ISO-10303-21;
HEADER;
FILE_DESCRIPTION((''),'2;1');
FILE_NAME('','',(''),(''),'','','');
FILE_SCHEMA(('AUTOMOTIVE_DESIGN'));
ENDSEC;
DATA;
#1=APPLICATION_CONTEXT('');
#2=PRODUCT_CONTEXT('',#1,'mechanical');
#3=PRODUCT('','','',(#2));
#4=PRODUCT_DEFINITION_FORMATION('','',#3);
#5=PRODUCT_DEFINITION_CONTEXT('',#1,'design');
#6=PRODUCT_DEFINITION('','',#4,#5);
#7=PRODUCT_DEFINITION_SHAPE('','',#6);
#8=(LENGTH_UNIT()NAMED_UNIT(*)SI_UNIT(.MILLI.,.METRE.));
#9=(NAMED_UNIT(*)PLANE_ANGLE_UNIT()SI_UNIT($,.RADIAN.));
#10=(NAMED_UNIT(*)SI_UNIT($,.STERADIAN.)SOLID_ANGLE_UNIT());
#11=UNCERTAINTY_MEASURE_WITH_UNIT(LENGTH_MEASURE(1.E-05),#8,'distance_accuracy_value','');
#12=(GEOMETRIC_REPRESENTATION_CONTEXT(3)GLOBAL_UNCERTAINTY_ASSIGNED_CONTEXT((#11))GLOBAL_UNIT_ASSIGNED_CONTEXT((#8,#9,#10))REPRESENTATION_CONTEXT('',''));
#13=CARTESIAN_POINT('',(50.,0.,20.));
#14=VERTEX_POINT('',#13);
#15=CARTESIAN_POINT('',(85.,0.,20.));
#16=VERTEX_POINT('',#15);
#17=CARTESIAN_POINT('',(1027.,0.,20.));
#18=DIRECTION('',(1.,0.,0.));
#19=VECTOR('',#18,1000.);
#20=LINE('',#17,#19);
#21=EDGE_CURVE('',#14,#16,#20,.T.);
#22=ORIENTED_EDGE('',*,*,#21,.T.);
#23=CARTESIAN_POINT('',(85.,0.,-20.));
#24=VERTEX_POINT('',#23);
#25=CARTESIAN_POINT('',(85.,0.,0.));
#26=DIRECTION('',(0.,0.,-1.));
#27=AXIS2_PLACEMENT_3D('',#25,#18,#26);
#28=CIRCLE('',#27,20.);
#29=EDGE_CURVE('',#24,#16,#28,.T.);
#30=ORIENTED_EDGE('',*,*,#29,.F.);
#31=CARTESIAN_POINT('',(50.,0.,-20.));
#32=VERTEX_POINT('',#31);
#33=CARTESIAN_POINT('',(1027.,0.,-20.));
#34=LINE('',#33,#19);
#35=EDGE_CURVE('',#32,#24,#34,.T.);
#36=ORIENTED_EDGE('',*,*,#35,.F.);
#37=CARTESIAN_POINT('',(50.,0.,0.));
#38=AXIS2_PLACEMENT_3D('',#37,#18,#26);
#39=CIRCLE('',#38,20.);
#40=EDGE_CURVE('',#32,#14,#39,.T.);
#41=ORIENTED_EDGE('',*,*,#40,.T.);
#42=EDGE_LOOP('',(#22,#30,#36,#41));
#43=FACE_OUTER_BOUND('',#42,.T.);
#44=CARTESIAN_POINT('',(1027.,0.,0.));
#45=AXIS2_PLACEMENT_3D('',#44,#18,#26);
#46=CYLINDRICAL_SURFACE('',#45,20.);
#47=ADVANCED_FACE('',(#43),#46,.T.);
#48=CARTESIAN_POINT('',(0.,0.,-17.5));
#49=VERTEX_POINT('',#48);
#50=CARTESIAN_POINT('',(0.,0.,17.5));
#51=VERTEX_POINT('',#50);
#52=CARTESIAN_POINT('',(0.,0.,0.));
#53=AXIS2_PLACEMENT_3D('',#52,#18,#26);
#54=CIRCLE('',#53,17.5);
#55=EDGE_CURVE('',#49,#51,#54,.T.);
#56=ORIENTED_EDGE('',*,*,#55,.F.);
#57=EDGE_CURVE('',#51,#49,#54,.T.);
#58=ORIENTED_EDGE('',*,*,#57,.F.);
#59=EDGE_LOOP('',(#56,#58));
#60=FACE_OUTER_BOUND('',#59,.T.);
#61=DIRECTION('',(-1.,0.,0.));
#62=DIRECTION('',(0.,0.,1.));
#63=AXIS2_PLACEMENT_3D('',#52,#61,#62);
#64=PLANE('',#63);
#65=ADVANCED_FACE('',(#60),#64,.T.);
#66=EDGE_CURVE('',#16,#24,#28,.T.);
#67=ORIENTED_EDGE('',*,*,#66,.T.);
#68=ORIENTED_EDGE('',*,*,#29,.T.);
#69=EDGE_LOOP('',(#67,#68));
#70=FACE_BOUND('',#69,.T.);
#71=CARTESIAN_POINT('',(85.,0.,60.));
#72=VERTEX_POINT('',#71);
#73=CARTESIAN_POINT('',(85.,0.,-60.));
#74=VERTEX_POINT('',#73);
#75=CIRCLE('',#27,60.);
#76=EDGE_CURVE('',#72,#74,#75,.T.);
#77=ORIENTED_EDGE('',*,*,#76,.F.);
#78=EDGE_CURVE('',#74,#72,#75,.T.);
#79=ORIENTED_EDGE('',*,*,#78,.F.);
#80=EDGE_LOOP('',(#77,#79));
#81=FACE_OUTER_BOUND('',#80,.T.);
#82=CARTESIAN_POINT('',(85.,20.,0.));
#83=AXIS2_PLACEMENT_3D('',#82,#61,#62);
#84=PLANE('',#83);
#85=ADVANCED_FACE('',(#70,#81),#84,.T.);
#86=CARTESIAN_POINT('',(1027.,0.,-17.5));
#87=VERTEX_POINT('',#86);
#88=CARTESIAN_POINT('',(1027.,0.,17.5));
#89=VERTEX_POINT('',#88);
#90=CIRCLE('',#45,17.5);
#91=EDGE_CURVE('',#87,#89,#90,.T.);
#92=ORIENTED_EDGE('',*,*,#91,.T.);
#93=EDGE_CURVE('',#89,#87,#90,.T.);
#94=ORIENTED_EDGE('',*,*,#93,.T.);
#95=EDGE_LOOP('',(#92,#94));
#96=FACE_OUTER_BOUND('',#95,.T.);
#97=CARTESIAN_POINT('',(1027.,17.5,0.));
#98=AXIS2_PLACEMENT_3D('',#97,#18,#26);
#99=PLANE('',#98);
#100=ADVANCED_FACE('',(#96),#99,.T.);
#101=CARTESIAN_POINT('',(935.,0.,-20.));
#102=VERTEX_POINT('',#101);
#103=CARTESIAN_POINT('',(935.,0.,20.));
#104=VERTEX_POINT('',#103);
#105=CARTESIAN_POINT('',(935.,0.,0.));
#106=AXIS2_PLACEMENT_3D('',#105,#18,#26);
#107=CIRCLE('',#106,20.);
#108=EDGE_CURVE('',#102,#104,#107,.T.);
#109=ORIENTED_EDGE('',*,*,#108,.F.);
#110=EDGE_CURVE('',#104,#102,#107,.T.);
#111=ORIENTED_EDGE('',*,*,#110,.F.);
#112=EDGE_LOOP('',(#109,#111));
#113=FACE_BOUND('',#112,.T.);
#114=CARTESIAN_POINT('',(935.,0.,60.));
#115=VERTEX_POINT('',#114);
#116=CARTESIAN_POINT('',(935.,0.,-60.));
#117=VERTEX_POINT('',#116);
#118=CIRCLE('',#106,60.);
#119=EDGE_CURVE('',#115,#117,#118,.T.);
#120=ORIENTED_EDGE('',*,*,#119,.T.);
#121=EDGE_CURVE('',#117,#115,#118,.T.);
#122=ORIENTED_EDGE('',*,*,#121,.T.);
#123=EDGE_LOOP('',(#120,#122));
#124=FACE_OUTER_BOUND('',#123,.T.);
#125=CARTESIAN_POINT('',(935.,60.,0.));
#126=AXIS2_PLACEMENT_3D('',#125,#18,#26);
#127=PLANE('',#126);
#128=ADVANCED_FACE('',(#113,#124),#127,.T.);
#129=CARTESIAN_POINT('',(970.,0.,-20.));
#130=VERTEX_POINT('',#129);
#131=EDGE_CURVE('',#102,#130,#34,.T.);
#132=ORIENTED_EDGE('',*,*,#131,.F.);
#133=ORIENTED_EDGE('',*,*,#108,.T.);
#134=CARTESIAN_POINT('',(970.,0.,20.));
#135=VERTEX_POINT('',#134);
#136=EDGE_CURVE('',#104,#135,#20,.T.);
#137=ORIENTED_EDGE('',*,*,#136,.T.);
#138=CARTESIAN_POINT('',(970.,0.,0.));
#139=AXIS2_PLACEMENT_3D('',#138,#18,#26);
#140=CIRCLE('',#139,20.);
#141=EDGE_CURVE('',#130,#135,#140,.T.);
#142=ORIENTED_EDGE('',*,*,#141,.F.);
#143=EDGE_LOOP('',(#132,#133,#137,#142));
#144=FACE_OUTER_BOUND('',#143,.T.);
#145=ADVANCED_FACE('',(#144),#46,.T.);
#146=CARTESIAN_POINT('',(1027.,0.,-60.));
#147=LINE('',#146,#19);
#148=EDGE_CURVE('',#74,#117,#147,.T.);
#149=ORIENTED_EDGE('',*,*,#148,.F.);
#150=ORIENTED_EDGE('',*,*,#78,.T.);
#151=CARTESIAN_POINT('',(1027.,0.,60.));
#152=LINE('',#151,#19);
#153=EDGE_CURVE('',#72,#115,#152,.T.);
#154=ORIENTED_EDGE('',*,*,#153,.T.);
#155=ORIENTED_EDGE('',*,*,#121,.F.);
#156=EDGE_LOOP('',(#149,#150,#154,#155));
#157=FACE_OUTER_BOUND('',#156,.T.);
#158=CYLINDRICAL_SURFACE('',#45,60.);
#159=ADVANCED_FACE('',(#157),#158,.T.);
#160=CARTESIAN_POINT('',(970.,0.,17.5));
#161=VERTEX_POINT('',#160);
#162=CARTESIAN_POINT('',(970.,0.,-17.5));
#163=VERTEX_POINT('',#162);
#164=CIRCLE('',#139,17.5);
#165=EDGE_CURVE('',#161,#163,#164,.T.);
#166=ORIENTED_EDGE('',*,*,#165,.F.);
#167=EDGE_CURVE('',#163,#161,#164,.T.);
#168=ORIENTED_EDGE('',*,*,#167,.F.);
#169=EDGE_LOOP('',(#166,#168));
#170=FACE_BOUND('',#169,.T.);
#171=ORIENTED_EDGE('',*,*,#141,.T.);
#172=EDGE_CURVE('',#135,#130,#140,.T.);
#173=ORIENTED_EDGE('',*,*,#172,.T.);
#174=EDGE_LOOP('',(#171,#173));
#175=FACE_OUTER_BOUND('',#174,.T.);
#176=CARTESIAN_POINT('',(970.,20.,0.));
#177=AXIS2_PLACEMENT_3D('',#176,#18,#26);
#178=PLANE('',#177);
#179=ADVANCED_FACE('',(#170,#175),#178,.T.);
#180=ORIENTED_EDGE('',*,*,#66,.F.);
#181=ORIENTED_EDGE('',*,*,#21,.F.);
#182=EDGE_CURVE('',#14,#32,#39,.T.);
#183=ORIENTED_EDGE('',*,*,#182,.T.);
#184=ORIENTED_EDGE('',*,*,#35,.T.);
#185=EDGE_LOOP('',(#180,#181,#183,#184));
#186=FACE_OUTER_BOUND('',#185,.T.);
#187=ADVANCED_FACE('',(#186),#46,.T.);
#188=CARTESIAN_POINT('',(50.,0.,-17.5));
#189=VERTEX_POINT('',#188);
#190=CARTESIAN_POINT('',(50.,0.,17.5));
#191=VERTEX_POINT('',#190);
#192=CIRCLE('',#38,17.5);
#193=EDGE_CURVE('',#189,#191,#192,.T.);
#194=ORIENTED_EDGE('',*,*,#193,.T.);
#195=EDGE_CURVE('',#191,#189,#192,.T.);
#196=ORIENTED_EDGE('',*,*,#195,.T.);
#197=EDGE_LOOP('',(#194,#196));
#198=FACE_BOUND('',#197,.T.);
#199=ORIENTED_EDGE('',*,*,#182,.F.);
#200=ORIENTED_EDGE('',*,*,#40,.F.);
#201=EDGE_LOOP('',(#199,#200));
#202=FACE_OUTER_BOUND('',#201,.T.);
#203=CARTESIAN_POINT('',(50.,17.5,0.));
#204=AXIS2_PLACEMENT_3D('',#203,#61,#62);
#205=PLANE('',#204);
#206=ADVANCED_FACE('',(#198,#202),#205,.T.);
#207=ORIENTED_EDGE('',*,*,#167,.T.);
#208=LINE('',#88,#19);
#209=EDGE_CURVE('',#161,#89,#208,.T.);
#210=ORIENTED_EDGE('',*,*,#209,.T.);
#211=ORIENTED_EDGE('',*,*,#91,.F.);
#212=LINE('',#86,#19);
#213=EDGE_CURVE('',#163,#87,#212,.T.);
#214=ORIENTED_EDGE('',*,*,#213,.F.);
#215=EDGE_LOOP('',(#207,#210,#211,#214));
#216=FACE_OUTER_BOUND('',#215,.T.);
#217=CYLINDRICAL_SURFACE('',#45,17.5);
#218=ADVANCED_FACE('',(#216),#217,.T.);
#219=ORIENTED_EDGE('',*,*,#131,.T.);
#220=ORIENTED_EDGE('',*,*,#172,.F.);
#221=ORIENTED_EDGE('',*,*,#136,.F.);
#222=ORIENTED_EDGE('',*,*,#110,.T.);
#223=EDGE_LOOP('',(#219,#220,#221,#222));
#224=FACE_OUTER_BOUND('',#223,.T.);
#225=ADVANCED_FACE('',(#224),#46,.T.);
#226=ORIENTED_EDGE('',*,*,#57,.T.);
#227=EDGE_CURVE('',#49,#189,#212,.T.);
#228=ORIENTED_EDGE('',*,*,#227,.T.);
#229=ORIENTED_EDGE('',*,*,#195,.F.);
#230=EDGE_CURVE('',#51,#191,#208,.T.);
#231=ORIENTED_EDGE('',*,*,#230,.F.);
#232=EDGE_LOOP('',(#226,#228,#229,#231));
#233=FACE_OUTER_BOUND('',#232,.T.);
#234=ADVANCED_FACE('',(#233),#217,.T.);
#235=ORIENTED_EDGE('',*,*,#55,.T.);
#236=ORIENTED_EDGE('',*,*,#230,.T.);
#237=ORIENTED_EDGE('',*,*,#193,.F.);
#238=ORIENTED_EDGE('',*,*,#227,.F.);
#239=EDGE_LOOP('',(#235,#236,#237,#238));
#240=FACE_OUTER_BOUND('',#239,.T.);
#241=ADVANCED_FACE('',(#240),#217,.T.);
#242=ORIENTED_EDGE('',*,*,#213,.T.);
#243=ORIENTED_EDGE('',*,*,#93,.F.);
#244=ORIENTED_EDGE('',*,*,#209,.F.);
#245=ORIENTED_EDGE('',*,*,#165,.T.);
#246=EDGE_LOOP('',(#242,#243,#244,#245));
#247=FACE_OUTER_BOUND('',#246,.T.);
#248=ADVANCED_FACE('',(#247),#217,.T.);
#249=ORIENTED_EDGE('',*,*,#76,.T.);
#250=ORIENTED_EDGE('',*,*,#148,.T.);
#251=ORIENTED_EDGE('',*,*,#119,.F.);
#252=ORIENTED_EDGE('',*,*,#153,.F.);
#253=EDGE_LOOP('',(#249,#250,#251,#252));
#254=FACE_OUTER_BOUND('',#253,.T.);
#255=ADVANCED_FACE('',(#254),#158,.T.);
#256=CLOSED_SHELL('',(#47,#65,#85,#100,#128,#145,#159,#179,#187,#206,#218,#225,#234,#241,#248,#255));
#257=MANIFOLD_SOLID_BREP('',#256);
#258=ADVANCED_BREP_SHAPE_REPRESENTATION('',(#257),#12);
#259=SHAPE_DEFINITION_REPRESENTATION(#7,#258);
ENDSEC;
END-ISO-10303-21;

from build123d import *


with BuildPart() as part:
    # 草图1 → 旋转1 (revolve)
    with BuildSketch(Plane.XY, mode=Mode.PRIVATE) as revolve_1_sk:
        Polygon((0, 0), (0, 17.5), (50, 17.5), (50, 20), (85, 20), (85, 60), (935, 60), (935, 20), (970, 20), (970, 17.5), (1027, 17.5), (1027, 0), align=None)
    revolve(revolve_1_sk.sketch.rotate(Axis((1027, 0, 0), (-1, 0, 0)), 90), axis=Axis((1027, 0, 0), (-1, 0, 0)))


solid = part.part
